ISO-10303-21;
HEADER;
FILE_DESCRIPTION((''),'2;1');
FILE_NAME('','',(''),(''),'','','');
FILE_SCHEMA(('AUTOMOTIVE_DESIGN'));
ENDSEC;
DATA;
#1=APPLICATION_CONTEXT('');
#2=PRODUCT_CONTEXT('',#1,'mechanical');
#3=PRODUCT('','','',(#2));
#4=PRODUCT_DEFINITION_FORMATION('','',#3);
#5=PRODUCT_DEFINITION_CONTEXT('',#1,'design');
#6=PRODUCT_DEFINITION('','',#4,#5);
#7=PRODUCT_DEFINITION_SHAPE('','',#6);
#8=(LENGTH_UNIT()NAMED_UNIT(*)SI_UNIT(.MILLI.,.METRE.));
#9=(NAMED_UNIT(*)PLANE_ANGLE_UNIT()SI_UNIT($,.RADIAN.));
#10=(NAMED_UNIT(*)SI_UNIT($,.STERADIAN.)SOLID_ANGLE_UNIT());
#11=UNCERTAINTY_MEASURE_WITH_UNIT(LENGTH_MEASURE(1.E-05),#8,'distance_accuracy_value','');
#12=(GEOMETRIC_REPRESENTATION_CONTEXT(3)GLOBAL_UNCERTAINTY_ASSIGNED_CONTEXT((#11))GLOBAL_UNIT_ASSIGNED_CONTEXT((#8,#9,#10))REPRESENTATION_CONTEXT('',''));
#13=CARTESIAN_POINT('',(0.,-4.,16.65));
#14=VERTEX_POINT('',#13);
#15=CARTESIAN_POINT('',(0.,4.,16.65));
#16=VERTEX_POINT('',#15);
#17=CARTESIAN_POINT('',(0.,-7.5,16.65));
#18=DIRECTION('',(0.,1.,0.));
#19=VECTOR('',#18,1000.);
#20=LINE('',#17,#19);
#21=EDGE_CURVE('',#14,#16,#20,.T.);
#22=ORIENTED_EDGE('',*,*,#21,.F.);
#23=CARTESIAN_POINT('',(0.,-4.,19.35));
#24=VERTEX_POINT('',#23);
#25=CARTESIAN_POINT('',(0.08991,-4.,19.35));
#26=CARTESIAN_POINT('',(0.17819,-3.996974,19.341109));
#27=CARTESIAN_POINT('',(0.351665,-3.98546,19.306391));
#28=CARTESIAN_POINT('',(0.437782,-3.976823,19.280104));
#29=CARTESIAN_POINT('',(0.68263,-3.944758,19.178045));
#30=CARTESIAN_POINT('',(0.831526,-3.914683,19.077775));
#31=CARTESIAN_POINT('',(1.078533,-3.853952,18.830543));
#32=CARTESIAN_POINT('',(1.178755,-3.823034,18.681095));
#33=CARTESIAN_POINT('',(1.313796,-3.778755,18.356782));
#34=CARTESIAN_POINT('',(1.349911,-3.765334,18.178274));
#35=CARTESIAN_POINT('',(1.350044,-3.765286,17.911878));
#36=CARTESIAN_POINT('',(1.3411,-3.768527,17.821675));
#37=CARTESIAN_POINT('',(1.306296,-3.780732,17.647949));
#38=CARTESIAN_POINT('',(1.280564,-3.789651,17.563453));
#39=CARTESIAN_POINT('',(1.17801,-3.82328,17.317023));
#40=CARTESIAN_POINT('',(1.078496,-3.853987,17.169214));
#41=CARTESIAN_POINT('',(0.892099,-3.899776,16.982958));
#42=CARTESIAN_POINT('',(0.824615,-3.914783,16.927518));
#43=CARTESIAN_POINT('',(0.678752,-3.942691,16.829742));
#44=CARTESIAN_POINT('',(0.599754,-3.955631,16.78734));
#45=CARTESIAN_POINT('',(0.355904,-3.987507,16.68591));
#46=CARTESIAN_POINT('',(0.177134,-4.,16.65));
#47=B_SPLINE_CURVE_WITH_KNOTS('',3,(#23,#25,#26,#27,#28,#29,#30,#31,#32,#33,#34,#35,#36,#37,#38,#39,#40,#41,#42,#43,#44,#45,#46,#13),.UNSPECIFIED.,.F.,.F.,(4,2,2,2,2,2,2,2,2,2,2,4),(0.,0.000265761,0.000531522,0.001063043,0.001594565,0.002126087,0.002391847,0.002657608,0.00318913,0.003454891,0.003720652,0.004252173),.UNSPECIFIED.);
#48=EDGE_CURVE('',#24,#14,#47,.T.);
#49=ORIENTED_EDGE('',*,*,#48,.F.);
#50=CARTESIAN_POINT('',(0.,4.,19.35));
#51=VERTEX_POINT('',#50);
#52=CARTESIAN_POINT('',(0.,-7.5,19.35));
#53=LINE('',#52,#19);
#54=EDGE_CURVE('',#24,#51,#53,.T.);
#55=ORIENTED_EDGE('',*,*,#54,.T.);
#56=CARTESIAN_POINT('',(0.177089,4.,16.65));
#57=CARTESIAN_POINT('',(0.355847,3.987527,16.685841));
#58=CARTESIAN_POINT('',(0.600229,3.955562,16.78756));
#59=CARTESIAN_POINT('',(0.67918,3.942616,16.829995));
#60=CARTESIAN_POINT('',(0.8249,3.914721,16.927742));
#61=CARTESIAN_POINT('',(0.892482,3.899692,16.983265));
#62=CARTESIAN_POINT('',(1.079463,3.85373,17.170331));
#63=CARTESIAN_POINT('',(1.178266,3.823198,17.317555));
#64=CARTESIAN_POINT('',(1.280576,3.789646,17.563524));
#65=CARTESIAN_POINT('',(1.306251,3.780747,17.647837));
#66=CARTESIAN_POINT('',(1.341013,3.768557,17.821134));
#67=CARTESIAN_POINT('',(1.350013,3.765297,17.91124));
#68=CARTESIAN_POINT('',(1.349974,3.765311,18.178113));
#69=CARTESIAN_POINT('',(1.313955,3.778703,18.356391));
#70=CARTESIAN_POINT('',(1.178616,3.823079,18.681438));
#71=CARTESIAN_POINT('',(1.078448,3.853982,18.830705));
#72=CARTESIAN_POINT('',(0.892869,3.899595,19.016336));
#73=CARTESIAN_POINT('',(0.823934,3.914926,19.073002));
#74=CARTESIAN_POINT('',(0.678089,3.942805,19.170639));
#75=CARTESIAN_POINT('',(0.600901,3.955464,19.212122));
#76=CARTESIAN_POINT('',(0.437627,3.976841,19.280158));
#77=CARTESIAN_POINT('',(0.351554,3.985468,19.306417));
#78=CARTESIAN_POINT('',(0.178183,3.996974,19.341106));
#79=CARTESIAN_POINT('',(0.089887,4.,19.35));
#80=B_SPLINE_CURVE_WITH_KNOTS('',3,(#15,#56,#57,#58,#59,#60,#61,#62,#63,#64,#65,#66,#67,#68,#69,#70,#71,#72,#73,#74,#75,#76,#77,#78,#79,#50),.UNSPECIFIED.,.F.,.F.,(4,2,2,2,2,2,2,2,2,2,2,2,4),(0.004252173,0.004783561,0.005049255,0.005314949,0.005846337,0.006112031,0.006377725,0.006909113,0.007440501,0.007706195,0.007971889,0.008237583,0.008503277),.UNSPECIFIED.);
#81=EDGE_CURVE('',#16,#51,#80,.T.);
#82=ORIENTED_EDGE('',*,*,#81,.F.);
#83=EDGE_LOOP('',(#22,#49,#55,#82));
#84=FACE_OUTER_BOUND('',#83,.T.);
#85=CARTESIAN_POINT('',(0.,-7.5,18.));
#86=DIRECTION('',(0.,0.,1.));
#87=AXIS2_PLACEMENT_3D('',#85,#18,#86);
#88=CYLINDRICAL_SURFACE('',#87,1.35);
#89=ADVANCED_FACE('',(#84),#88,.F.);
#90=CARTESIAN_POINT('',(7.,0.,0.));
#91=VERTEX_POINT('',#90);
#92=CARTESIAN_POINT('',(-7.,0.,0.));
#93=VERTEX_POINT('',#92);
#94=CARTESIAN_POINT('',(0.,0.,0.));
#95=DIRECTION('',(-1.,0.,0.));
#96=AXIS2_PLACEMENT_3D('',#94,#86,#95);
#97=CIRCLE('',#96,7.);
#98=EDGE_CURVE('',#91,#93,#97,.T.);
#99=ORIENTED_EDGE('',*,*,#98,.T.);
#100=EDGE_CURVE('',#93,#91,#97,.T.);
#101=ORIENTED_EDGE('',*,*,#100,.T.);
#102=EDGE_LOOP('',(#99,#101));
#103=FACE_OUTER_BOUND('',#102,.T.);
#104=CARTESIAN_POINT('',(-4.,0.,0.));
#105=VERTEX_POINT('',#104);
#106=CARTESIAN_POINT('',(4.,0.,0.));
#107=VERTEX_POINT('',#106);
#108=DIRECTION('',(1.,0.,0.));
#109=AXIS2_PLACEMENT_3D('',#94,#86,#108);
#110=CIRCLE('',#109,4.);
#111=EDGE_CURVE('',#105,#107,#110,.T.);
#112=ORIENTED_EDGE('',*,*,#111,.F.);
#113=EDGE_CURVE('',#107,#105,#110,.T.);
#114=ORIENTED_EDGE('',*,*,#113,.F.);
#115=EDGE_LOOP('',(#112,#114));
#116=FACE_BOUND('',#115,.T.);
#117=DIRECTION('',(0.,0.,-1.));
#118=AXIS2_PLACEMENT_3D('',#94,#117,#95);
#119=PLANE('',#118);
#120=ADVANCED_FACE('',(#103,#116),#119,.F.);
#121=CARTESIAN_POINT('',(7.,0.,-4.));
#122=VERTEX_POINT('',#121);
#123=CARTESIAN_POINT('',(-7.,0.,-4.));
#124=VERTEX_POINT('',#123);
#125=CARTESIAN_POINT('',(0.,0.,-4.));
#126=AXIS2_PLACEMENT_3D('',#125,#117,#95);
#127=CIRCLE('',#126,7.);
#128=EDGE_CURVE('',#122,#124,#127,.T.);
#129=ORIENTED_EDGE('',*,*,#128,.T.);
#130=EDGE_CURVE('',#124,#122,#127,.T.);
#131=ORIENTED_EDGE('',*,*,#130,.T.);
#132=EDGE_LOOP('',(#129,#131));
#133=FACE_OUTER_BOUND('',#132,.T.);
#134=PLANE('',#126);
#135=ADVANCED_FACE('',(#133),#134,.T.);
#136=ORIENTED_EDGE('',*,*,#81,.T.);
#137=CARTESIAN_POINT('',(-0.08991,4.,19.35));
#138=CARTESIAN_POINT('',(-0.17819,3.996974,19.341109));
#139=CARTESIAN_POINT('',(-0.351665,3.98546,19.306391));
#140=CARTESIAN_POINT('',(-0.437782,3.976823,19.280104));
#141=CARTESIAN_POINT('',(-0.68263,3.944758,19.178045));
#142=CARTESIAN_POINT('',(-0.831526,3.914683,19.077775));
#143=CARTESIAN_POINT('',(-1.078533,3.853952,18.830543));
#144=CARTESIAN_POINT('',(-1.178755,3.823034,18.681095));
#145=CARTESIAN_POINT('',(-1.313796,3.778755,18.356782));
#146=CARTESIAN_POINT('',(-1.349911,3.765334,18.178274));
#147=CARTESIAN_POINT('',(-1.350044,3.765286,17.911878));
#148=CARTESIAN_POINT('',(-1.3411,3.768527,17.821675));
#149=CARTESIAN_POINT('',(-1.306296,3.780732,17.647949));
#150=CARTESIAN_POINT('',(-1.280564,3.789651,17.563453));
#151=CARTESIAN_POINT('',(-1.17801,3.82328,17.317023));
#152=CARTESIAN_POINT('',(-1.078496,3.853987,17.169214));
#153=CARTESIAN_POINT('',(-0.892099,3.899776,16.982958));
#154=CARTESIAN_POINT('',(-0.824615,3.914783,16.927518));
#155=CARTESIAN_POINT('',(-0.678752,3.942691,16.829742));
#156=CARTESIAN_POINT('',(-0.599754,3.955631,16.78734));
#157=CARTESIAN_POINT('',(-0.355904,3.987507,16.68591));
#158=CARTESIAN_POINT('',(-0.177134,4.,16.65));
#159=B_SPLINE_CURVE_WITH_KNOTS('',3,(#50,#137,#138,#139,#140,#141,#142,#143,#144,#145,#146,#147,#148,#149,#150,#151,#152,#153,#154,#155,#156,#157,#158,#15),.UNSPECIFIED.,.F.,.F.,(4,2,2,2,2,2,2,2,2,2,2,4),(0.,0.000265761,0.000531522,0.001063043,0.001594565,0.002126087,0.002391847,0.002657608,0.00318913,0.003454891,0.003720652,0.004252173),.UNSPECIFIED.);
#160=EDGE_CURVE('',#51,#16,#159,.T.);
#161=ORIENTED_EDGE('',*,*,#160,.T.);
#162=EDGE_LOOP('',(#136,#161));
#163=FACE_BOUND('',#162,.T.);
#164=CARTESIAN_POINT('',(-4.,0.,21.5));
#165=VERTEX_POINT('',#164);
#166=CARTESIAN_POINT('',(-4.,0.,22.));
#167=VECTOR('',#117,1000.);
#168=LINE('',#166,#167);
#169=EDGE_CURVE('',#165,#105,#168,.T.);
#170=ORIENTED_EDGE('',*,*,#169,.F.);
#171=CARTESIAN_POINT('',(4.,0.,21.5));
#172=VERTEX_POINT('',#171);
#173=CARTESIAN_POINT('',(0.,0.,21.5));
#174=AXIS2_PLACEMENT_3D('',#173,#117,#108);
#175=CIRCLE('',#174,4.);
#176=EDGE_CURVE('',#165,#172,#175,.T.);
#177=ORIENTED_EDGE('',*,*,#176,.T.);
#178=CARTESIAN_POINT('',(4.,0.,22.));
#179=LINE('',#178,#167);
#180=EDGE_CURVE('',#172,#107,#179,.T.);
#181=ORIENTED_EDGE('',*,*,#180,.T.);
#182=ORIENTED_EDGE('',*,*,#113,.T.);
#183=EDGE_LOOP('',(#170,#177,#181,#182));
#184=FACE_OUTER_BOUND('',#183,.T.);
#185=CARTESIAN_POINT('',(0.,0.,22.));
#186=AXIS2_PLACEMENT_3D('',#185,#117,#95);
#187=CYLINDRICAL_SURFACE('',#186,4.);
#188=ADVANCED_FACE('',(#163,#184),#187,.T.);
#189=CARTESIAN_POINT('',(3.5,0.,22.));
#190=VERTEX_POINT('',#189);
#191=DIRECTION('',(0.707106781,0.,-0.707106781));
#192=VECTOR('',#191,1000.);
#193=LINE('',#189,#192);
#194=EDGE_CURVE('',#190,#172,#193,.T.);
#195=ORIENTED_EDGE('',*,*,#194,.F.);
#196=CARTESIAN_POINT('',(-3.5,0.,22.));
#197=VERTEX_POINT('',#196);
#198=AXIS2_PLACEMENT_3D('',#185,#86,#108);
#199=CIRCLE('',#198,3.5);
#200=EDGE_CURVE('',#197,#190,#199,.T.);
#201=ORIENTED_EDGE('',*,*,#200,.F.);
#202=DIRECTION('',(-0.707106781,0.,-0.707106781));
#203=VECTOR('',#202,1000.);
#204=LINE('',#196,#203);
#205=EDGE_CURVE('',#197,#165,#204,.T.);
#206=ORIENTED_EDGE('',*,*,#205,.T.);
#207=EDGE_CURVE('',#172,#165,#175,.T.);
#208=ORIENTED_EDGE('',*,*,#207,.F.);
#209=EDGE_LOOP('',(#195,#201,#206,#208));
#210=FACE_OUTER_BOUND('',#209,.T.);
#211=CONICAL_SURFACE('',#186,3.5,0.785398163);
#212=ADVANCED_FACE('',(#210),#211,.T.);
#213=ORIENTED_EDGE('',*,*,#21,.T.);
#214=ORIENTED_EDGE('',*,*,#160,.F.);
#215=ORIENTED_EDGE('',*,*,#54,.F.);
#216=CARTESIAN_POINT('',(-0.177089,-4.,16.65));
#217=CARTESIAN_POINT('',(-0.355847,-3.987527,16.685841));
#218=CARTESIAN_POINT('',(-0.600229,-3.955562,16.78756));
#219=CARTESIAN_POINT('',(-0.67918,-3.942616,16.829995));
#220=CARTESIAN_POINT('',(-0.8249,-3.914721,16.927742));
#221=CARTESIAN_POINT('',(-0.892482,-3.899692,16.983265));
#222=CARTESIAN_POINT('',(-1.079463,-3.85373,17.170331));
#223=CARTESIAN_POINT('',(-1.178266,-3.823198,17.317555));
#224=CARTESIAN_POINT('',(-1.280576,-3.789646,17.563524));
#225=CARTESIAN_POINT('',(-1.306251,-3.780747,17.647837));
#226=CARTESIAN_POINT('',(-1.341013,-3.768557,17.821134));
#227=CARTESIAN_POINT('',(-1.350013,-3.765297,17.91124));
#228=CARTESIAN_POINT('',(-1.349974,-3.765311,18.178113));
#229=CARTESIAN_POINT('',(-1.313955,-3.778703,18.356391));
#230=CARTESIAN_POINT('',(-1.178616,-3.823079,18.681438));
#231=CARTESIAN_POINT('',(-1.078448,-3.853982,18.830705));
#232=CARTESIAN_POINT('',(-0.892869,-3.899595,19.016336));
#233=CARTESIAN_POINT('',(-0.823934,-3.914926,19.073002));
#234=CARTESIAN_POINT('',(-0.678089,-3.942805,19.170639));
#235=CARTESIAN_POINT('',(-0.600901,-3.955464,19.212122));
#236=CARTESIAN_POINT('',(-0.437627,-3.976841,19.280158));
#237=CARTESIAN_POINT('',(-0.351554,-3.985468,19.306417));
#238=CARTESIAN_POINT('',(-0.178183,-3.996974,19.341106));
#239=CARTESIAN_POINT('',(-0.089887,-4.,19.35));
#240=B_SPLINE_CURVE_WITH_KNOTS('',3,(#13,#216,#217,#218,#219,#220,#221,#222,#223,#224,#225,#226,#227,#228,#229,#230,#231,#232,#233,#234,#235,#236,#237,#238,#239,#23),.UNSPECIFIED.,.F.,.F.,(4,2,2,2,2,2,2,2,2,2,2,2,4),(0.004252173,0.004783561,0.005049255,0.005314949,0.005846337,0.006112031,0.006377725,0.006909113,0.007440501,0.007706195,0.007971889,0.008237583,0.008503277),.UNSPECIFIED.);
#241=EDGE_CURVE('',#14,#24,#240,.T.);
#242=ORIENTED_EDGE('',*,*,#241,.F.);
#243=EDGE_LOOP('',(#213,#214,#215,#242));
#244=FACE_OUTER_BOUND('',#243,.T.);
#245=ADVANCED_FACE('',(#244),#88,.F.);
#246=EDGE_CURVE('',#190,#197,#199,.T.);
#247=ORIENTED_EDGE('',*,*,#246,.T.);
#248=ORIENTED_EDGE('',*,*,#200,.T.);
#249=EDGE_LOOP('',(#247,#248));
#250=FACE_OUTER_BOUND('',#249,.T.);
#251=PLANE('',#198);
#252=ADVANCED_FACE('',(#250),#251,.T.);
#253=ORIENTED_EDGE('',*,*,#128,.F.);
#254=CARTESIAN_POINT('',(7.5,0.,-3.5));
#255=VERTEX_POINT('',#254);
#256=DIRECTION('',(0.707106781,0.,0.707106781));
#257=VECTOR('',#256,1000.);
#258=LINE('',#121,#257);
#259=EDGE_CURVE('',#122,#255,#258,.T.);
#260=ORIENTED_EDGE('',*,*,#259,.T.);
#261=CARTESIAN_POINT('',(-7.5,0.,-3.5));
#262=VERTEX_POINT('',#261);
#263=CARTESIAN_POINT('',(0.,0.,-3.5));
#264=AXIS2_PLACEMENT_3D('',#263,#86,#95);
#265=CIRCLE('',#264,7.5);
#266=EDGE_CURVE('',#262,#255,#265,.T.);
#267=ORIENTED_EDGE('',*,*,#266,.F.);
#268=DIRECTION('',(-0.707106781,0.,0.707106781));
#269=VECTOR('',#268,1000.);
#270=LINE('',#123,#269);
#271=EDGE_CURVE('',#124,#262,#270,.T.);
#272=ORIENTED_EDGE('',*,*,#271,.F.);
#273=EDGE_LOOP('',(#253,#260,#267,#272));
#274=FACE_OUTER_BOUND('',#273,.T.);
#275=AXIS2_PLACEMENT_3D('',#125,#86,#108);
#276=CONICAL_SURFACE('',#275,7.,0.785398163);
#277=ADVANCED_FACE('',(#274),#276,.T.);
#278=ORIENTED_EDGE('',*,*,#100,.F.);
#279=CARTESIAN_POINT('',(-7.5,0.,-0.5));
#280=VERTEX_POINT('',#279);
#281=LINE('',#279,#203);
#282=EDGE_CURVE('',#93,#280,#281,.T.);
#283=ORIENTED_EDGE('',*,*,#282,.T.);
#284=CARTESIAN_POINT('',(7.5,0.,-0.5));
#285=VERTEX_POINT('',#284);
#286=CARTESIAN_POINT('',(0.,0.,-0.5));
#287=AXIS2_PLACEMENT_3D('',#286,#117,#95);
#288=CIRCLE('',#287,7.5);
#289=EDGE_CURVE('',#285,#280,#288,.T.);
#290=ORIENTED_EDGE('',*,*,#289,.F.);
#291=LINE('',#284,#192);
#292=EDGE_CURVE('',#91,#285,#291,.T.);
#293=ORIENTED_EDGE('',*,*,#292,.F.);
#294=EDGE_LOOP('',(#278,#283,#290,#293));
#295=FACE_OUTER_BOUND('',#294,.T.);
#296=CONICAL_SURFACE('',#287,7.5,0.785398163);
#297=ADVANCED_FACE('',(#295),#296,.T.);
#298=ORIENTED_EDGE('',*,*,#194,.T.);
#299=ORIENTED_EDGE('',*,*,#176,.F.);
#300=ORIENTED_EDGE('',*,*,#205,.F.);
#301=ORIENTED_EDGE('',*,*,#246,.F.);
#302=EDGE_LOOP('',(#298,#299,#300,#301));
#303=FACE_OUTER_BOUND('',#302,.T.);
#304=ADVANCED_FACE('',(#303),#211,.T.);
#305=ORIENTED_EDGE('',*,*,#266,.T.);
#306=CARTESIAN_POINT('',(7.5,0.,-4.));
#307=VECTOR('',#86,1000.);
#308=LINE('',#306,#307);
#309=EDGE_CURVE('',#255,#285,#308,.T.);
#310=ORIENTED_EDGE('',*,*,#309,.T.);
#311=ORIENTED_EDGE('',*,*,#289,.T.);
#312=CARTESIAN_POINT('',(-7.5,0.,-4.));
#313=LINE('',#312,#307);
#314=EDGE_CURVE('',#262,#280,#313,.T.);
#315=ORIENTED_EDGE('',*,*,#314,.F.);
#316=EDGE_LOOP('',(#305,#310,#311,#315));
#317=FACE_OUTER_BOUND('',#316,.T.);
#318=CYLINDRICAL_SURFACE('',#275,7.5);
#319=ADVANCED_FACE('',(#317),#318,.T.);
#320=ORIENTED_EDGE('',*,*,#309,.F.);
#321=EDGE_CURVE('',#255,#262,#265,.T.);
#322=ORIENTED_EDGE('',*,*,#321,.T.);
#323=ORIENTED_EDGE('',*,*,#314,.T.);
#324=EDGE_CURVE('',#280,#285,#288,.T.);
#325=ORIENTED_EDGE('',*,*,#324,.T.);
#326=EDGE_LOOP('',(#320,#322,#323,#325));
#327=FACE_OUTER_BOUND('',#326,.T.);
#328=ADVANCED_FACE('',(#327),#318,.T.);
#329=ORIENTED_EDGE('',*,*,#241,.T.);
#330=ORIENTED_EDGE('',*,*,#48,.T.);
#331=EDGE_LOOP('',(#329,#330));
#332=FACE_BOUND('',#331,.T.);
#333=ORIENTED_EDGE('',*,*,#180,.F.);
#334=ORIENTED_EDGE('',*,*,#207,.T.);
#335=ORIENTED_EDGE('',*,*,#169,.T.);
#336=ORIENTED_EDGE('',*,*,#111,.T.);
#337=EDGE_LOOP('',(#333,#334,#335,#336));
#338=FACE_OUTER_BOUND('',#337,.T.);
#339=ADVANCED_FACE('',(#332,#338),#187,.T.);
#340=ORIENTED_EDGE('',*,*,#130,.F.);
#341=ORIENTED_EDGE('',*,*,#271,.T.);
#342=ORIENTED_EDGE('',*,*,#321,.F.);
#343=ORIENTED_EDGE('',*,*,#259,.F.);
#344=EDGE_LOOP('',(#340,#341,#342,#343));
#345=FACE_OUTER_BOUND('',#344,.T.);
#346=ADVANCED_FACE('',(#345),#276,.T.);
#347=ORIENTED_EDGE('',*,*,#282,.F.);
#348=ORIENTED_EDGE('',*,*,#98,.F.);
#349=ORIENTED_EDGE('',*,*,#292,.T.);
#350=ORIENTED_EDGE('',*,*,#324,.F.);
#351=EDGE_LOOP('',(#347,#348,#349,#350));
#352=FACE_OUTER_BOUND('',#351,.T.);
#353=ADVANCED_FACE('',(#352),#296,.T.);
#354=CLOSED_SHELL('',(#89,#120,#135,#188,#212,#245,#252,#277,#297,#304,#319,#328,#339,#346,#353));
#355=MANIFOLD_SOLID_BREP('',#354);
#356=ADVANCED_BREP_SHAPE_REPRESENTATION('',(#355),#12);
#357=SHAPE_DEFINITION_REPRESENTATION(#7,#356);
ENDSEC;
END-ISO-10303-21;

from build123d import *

# Parameters (mm, degrees)
SKETCH1_R               = 4
BOSS_EXTRUDE1_DEPTH     = 22
SKETCH2_R               = 7.5
BOSS_EXTRUDE2_DEPTH     = 4
CUT_EXTRUDE1_DEPTH      = 25.423349484
CUT_EXTRUDE1_DEPTH_BACK = 25.423349484
SKETCH3_R               = 1.35
CHAMFER1_SIZE           = 0.5


with BuildPart() as part:
    # Sketch1 → Boss-Extrude1 (new body)
    with BuildSketch(Plane.XY):
        Circle(SKETCH1_R)
    extrude(amount=BOSS_EXTRUDE1_DEPTH)

    # Sketch2 → Boss-Extrude2 (add)
    with BuildSketch(Plane(origin=(0, 0, 0), x_dir=(-1, 0, 0), z_dir=(0, 0, -1))):
        Circle(SKETCH2_R)
    extrude(amount=BOSS_EXTRUDE2_DEPTH)

    # Sketch3 → Cut-Extrude1 (cut, two sides: drawn at the far end of the back side and taken through both)
    with BuildSketch(Plane(origin=(0, 0, 0), x_dir=(1, 0, 0), z_dir=(0, 1, 0)).offset(-CUT_EXTRUDE1_DEPTH_BACK)):
        with Locations(Location((0, -18, 0), (0, 0, 270))):
            Circle(SKETCH3_R)
    extrude(amount=CUT_EXTRUDE1_DEPTH + CUT_EXTRUDE1_DEPTH_BACK, mode=Mode.SUBTRACT)

    # Chamfer1
    chamfer1_edges = [part.edges().sort_by_distance(p)[0] for p in [
        (-4, 0, 22),
        (7.5, 0, 0),
        (7.5, 0, -4),
    ]]
    chamfer(chamfer1_edges, length=CHAMFER1_SIZE)


solid = part.part
